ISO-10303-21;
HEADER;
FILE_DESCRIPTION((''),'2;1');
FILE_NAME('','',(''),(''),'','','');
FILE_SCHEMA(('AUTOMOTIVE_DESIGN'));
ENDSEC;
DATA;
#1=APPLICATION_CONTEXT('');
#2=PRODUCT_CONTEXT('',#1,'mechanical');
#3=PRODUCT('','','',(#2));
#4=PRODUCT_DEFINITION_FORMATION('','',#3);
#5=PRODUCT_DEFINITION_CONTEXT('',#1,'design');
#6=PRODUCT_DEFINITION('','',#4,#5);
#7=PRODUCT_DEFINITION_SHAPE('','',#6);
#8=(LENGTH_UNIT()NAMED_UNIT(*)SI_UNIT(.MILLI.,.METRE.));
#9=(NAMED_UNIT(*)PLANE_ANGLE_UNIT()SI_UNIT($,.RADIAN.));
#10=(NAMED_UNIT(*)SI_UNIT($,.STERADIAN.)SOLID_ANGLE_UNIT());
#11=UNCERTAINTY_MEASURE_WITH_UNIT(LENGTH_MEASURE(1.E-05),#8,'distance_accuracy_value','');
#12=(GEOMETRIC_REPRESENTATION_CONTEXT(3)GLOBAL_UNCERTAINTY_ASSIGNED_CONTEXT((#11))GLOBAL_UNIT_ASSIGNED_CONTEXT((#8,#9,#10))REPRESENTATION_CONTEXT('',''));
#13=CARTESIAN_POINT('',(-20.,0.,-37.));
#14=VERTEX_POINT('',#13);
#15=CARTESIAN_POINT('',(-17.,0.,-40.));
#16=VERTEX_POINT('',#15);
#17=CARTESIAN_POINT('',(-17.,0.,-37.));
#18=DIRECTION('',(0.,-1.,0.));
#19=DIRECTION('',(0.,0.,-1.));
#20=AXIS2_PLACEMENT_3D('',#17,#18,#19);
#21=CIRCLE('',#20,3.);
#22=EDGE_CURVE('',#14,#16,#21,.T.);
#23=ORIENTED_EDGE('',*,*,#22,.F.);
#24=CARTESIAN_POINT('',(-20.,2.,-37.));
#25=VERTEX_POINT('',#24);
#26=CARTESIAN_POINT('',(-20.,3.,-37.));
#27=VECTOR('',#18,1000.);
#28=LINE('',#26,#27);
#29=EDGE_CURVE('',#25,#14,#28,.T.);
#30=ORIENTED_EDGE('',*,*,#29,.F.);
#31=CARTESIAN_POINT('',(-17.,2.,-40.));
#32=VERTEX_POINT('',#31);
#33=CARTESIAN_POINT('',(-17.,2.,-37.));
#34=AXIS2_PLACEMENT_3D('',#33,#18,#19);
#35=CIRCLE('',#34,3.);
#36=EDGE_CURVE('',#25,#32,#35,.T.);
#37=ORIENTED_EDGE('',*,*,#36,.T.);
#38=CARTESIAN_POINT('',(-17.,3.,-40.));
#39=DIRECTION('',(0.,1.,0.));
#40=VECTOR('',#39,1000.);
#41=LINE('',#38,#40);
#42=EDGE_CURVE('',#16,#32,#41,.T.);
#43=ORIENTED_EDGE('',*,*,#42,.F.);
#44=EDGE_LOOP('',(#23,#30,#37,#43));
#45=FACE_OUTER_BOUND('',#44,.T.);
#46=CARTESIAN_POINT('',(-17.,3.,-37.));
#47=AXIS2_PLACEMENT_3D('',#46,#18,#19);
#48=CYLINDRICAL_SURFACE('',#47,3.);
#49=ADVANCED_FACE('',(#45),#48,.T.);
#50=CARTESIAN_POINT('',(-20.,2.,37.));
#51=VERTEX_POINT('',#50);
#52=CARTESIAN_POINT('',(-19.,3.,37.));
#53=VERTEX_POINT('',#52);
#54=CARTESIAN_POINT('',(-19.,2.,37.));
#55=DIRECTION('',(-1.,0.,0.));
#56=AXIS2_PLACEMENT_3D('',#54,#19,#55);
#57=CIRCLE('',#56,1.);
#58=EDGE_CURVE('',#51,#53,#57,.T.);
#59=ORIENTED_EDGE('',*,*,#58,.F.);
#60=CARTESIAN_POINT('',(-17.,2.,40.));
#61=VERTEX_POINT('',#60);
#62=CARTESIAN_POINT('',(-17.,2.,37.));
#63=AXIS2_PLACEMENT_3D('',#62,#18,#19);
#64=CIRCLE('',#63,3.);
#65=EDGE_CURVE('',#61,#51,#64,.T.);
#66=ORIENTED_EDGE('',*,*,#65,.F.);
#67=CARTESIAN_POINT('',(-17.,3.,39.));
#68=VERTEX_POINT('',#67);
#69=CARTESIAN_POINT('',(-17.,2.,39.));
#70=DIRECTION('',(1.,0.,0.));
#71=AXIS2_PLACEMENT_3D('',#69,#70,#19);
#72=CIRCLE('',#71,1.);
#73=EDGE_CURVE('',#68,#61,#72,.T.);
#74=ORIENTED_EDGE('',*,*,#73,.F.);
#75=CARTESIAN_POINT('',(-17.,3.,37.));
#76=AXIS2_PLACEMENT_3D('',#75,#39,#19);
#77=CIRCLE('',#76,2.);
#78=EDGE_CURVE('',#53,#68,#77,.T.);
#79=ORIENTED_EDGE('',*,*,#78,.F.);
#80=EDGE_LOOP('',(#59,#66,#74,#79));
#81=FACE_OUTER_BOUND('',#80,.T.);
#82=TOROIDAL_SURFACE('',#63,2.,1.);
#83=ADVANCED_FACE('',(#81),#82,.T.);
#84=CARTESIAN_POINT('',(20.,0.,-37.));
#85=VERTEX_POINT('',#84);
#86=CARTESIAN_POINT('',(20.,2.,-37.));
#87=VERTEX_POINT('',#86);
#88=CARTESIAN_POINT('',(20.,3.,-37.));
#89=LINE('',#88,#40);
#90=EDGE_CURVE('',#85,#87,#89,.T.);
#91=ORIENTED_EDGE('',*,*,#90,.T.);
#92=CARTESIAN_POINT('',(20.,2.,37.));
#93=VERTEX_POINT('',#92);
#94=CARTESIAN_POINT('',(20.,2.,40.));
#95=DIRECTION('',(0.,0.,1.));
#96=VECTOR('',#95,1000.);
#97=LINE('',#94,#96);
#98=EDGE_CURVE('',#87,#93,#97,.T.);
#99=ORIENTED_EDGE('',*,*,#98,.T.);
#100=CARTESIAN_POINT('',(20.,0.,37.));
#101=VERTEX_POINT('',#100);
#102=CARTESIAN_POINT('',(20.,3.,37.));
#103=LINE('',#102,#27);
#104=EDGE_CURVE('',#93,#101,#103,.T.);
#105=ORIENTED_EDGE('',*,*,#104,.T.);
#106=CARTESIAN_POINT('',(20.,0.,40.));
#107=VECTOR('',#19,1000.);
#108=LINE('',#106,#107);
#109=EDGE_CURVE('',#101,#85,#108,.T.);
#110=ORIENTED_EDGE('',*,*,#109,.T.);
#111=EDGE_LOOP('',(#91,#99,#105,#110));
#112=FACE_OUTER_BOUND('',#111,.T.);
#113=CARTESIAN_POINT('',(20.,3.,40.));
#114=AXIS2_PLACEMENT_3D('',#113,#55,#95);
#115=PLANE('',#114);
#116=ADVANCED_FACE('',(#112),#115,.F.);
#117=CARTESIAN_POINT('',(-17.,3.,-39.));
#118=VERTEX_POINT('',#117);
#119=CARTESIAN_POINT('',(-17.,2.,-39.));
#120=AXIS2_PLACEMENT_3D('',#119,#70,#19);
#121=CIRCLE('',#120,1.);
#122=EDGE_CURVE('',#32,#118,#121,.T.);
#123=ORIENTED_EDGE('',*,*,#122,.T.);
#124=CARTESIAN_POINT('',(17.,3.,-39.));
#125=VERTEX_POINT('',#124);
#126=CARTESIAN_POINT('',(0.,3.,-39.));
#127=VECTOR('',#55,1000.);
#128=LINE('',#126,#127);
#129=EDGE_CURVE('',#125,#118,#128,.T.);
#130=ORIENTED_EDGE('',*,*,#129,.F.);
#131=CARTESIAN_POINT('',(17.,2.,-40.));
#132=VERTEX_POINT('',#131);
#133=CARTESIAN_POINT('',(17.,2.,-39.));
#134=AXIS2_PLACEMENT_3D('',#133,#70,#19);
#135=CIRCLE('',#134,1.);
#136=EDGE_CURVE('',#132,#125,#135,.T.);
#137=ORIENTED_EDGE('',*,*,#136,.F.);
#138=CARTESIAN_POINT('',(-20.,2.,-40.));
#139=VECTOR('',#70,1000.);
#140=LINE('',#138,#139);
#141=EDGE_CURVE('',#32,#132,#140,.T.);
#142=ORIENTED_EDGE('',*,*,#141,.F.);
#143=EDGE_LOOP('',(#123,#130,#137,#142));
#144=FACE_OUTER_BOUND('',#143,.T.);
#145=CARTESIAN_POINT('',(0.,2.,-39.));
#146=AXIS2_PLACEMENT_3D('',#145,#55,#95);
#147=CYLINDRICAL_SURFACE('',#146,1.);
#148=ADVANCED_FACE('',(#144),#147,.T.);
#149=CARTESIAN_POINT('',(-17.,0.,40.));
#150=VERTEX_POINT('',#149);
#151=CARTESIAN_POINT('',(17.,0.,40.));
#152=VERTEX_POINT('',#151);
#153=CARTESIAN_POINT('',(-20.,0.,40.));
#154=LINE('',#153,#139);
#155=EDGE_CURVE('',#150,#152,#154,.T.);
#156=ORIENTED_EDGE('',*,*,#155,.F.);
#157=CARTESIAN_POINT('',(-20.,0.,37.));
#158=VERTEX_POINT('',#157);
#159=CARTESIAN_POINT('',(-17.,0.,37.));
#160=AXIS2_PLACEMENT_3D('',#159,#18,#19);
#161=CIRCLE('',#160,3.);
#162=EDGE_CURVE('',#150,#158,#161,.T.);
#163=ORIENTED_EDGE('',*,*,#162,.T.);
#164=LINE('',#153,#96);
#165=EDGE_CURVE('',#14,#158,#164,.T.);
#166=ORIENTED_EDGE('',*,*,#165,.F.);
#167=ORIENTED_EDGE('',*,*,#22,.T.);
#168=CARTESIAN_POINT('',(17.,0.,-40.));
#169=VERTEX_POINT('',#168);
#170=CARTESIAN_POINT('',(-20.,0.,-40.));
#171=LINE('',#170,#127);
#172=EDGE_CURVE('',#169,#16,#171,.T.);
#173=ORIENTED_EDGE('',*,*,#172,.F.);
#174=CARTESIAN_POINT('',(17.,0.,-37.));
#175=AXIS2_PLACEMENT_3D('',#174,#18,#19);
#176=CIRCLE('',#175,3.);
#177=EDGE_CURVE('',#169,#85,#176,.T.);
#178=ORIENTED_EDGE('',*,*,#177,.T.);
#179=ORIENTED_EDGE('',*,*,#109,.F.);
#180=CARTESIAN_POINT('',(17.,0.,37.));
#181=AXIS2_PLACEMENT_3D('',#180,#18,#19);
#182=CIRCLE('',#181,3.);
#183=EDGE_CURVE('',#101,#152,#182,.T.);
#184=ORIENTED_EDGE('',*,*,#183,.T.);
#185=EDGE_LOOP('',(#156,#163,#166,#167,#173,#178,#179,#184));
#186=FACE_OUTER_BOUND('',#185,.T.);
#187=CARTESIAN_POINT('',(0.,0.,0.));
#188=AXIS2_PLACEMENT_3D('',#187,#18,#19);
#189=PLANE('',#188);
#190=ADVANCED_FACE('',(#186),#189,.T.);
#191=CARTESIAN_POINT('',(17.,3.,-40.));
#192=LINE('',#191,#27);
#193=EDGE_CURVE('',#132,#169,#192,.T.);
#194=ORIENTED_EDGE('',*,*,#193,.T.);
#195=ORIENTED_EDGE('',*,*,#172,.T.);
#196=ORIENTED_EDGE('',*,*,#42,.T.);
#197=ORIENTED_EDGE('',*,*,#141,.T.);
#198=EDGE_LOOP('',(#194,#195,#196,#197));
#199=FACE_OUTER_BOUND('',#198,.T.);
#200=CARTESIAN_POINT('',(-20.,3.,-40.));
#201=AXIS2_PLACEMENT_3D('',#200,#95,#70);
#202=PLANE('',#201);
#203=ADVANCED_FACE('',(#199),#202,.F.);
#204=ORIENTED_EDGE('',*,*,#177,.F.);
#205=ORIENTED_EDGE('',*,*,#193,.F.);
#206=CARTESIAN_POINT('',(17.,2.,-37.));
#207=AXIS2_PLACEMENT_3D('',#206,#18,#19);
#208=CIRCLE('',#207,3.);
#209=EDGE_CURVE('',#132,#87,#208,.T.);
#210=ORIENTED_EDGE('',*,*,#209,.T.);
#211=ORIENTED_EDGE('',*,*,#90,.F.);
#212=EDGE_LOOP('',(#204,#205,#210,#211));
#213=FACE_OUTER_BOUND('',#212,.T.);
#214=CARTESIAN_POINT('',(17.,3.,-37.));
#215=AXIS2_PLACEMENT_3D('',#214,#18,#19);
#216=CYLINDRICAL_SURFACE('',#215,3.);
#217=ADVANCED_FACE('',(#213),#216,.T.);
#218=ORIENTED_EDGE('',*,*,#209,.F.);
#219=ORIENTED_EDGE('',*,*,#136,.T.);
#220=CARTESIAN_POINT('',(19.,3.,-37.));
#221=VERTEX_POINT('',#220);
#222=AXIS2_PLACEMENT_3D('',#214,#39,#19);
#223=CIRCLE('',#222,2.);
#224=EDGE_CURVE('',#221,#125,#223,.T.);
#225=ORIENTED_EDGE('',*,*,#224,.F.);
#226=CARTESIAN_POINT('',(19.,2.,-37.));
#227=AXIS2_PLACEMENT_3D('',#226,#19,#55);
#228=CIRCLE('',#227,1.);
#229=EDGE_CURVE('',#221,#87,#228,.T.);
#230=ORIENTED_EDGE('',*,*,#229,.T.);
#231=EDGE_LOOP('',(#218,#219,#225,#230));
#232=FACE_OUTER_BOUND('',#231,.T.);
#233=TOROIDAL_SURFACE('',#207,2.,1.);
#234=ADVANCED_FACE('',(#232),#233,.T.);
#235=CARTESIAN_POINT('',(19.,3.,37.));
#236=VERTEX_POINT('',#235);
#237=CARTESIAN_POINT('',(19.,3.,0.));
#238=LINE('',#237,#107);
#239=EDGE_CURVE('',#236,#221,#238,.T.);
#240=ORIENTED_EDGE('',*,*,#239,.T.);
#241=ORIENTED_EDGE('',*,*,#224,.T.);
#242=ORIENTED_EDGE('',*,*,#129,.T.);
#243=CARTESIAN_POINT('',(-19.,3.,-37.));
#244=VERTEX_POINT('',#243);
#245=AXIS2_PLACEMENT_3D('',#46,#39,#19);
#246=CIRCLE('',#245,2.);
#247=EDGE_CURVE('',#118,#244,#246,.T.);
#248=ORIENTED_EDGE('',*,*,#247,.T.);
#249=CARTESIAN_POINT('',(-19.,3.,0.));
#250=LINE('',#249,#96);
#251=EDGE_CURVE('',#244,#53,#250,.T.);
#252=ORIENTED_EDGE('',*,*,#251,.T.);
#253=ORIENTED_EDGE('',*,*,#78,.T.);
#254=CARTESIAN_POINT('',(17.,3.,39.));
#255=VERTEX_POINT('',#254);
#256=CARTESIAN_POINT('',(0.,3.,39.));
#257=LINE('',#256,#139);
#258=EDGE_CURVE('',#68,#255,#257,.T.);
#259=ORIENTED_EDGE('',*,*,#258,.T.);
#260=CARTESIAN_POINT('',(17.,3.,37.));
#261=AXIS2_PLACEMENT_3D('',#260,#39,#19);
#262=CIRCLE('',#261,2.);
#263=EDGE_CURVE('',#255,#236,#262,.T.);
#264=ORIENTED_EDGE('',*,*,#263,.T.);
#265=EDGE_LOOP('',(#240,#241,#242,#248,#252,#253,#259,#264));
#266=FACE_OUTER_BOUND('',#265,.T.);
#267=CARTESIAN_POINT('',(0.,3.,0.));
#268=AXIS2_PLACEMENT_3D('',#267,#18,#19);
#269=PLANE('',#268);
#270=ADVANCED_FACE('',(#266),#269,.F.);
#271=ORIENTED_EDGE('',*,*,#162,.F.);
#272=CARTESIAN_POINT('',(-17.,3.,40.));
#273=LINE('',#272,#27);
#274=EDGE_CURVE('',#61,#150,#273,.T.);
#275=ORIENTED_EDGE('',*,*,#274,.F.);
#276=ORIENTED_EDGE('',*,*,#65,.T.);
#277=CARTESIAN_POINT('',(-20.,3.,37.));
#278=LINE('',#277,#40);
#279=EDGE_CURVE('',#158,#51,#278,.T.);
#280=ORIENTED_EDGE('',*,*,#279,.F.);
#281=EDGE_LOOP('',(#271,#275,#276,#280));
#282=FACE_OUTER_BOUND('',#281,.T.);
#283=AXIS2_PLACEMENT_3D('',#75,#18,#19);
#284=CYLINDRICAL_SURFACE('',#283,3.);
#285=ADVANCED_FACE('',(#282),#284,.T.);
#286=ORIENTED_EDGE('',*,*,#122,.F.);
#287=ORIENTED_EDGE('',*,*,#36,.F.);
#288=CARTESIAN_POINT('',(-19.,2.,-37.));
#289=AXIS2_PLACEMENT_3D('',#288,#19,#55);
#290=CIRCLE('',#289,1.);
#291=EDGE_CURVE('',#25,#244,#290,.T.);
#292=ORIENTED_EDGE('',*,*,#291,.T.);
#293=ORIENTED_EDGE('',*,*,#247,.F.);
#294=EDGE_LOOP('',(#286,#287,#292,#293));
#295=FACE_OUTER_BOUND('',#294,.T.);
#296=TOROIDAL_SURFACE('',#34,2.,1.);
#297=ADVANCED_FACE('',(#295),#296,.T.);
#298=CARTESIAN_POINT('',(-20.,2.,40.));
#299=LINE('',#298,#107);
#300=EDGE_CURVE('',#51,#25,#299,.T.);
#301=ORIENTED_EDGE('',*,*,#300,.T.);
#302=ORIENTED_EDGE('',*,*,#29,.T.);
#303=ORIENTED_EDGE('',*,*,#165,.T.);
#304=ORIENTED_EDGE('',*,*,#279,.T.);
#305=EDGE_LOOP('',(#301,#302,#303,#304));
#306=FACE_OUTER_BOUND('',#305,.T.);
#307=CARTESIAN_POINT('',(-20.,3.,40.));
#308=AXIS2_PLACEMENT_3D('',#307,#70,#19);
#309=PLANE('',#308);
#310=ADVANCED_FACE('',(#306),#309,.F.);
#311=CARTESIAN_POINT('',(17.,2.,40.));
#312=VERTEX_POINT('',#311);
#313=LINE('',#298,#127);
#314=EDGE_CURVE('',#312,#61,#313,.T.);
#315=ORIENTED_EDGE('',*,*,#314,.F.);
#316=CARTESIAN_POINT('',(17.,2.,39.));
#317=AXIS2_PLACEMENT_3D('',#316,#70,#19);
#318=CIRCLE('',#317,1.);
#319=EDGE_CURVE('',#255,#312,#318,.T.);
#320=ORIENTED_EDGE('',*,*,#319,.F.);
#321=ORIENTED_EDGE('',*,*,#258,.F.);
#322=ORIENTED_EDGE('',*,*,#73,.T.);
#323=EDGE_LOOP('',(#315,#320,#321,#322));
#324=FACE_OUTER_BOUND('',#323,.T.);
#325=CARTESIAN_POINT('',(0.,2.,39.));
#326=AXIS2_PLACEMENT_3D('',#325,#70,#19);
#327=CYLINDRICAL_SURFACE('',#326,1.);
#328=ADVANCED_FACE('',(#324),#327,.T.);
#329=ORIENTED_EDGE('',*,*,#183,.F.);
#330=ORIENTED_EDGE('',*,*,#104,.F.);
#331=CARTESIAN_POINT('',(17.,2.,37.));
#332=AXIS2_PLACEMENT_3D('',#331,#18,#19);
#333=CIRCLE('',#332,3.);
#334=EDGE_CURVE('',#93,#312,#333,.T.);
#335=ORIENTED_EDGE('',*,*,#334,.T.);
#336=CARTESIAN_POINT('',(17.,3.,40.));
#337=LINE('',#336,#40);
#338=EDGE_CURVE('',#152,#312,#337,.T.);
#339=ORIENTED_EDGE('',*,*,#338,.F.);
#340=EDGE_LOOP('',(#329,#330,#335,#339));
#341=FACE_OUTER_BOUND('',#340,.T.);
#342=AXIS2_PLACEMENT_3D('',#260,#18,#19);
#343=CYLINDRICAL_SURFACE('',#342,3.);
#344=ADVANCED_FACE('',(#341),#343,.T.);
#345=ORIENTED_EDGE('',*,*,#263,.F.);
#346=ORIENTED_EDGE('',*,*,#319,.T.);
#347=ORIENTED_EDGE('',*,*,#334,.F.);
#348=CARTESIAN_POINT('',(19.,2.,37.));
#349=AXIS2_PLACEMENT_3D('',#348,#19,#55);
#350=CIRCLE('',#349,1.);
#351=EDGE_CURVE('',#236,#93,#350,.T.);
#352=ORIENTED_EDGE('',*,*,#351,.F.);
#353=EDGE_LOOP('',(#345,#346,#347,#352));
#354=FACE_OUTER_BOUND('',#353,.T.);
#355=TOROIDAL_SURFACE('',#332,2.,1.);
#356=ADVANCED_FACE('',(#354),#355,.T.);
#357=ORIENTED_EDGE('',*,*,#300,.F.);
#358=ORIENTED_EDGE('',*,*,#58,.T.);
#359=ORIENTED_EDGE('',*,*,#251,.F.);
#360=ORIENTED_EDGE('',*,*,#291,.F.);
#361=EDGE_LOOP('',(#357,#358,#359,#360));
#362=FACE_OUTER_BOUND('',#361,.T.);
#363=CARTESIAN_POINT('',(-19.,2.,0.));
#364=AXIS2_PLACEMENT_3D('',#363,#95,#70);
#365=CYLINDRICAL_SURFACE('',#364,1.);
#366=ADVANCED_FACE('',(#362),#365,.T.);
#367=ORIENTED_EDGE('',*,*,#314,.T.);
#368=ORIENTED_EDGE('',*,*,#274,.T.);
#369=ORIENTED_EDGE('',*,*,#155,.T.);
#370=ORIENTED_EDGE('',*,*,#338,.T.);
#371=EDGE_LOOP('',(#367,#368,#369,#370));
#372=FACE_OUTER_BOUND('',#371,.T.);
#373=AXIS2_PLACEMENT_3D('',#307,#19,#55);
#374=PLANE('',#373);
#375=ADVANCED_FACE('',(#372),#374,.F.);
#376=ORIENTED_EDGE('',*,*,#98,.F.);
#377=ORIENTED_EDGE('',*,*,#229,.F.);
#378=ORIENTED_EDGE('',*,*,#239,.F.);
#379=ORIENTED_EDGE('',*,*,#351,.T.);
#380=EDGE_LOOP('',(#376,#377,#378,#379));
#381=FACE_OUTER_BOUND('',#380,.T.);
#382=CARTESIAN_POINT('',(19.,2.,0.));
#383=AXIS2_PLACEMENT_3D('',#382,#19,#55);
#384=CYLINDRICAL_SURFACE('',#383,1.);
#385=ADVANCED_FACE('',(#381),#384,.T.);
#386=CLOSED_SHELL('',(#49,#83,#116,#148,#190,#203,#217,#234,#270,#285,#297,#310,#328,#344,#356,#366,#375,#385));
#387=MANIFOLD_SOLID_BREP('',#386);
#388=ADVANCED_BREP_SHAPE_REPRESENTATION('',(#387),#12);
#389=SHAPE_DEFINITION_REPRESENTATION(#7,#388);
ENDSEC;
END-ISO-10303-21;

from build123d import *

# Parameters (mm, degrees)
SKETCH_1_W      = 40
SKETCH_1_H      = 80
EXTRUDE_1_DEPTH = 3
FILLET_2_R      = 3
FILLET_3_R      = 1


with BuildPart() as part:
    # 草图1 → 凸台-拉伸1 (new body)
    with BuildSketch(Plane(origin=(0, 0, 0), x_dir=(1, 0, 0), z_dir=(0, 1, 0))):
        Rectangle(SKETCH_1_W, SKETCH_1_H)
    extrude(amount=EXTRUDE_1_DEPTH)

    # 圆角2
    fillet_2_edges = [part.edges().sort_by_distance(p)[0] for p in [
        (20, 1.5, 40),
        (-20, 1.5, 40),
        (-20, 1.5, -40),
        (20, 1.5, -40),
    ]]
    fillet(fillet_2_edges, radius=FILLET_2_R)

    # 圆角3
    fillet_3_edges = [part.edges().sort_by_distance(p)[0] for p in [
        (-20, 3, 0),
        (0, 3, -40),
        (20, 3, 0),
        (0, 3, 40),
        (19.121320344, 3, 39.121320344),
        (-19.121320344, 3, 39.121320344),
        (19.121320344, 3, -39.121320344),
        (-19.121320344, 3, -39.121320344),
    ]]
    fillet(fillet_3_edges, radius=FILLET_3_R)


solid = part.part
